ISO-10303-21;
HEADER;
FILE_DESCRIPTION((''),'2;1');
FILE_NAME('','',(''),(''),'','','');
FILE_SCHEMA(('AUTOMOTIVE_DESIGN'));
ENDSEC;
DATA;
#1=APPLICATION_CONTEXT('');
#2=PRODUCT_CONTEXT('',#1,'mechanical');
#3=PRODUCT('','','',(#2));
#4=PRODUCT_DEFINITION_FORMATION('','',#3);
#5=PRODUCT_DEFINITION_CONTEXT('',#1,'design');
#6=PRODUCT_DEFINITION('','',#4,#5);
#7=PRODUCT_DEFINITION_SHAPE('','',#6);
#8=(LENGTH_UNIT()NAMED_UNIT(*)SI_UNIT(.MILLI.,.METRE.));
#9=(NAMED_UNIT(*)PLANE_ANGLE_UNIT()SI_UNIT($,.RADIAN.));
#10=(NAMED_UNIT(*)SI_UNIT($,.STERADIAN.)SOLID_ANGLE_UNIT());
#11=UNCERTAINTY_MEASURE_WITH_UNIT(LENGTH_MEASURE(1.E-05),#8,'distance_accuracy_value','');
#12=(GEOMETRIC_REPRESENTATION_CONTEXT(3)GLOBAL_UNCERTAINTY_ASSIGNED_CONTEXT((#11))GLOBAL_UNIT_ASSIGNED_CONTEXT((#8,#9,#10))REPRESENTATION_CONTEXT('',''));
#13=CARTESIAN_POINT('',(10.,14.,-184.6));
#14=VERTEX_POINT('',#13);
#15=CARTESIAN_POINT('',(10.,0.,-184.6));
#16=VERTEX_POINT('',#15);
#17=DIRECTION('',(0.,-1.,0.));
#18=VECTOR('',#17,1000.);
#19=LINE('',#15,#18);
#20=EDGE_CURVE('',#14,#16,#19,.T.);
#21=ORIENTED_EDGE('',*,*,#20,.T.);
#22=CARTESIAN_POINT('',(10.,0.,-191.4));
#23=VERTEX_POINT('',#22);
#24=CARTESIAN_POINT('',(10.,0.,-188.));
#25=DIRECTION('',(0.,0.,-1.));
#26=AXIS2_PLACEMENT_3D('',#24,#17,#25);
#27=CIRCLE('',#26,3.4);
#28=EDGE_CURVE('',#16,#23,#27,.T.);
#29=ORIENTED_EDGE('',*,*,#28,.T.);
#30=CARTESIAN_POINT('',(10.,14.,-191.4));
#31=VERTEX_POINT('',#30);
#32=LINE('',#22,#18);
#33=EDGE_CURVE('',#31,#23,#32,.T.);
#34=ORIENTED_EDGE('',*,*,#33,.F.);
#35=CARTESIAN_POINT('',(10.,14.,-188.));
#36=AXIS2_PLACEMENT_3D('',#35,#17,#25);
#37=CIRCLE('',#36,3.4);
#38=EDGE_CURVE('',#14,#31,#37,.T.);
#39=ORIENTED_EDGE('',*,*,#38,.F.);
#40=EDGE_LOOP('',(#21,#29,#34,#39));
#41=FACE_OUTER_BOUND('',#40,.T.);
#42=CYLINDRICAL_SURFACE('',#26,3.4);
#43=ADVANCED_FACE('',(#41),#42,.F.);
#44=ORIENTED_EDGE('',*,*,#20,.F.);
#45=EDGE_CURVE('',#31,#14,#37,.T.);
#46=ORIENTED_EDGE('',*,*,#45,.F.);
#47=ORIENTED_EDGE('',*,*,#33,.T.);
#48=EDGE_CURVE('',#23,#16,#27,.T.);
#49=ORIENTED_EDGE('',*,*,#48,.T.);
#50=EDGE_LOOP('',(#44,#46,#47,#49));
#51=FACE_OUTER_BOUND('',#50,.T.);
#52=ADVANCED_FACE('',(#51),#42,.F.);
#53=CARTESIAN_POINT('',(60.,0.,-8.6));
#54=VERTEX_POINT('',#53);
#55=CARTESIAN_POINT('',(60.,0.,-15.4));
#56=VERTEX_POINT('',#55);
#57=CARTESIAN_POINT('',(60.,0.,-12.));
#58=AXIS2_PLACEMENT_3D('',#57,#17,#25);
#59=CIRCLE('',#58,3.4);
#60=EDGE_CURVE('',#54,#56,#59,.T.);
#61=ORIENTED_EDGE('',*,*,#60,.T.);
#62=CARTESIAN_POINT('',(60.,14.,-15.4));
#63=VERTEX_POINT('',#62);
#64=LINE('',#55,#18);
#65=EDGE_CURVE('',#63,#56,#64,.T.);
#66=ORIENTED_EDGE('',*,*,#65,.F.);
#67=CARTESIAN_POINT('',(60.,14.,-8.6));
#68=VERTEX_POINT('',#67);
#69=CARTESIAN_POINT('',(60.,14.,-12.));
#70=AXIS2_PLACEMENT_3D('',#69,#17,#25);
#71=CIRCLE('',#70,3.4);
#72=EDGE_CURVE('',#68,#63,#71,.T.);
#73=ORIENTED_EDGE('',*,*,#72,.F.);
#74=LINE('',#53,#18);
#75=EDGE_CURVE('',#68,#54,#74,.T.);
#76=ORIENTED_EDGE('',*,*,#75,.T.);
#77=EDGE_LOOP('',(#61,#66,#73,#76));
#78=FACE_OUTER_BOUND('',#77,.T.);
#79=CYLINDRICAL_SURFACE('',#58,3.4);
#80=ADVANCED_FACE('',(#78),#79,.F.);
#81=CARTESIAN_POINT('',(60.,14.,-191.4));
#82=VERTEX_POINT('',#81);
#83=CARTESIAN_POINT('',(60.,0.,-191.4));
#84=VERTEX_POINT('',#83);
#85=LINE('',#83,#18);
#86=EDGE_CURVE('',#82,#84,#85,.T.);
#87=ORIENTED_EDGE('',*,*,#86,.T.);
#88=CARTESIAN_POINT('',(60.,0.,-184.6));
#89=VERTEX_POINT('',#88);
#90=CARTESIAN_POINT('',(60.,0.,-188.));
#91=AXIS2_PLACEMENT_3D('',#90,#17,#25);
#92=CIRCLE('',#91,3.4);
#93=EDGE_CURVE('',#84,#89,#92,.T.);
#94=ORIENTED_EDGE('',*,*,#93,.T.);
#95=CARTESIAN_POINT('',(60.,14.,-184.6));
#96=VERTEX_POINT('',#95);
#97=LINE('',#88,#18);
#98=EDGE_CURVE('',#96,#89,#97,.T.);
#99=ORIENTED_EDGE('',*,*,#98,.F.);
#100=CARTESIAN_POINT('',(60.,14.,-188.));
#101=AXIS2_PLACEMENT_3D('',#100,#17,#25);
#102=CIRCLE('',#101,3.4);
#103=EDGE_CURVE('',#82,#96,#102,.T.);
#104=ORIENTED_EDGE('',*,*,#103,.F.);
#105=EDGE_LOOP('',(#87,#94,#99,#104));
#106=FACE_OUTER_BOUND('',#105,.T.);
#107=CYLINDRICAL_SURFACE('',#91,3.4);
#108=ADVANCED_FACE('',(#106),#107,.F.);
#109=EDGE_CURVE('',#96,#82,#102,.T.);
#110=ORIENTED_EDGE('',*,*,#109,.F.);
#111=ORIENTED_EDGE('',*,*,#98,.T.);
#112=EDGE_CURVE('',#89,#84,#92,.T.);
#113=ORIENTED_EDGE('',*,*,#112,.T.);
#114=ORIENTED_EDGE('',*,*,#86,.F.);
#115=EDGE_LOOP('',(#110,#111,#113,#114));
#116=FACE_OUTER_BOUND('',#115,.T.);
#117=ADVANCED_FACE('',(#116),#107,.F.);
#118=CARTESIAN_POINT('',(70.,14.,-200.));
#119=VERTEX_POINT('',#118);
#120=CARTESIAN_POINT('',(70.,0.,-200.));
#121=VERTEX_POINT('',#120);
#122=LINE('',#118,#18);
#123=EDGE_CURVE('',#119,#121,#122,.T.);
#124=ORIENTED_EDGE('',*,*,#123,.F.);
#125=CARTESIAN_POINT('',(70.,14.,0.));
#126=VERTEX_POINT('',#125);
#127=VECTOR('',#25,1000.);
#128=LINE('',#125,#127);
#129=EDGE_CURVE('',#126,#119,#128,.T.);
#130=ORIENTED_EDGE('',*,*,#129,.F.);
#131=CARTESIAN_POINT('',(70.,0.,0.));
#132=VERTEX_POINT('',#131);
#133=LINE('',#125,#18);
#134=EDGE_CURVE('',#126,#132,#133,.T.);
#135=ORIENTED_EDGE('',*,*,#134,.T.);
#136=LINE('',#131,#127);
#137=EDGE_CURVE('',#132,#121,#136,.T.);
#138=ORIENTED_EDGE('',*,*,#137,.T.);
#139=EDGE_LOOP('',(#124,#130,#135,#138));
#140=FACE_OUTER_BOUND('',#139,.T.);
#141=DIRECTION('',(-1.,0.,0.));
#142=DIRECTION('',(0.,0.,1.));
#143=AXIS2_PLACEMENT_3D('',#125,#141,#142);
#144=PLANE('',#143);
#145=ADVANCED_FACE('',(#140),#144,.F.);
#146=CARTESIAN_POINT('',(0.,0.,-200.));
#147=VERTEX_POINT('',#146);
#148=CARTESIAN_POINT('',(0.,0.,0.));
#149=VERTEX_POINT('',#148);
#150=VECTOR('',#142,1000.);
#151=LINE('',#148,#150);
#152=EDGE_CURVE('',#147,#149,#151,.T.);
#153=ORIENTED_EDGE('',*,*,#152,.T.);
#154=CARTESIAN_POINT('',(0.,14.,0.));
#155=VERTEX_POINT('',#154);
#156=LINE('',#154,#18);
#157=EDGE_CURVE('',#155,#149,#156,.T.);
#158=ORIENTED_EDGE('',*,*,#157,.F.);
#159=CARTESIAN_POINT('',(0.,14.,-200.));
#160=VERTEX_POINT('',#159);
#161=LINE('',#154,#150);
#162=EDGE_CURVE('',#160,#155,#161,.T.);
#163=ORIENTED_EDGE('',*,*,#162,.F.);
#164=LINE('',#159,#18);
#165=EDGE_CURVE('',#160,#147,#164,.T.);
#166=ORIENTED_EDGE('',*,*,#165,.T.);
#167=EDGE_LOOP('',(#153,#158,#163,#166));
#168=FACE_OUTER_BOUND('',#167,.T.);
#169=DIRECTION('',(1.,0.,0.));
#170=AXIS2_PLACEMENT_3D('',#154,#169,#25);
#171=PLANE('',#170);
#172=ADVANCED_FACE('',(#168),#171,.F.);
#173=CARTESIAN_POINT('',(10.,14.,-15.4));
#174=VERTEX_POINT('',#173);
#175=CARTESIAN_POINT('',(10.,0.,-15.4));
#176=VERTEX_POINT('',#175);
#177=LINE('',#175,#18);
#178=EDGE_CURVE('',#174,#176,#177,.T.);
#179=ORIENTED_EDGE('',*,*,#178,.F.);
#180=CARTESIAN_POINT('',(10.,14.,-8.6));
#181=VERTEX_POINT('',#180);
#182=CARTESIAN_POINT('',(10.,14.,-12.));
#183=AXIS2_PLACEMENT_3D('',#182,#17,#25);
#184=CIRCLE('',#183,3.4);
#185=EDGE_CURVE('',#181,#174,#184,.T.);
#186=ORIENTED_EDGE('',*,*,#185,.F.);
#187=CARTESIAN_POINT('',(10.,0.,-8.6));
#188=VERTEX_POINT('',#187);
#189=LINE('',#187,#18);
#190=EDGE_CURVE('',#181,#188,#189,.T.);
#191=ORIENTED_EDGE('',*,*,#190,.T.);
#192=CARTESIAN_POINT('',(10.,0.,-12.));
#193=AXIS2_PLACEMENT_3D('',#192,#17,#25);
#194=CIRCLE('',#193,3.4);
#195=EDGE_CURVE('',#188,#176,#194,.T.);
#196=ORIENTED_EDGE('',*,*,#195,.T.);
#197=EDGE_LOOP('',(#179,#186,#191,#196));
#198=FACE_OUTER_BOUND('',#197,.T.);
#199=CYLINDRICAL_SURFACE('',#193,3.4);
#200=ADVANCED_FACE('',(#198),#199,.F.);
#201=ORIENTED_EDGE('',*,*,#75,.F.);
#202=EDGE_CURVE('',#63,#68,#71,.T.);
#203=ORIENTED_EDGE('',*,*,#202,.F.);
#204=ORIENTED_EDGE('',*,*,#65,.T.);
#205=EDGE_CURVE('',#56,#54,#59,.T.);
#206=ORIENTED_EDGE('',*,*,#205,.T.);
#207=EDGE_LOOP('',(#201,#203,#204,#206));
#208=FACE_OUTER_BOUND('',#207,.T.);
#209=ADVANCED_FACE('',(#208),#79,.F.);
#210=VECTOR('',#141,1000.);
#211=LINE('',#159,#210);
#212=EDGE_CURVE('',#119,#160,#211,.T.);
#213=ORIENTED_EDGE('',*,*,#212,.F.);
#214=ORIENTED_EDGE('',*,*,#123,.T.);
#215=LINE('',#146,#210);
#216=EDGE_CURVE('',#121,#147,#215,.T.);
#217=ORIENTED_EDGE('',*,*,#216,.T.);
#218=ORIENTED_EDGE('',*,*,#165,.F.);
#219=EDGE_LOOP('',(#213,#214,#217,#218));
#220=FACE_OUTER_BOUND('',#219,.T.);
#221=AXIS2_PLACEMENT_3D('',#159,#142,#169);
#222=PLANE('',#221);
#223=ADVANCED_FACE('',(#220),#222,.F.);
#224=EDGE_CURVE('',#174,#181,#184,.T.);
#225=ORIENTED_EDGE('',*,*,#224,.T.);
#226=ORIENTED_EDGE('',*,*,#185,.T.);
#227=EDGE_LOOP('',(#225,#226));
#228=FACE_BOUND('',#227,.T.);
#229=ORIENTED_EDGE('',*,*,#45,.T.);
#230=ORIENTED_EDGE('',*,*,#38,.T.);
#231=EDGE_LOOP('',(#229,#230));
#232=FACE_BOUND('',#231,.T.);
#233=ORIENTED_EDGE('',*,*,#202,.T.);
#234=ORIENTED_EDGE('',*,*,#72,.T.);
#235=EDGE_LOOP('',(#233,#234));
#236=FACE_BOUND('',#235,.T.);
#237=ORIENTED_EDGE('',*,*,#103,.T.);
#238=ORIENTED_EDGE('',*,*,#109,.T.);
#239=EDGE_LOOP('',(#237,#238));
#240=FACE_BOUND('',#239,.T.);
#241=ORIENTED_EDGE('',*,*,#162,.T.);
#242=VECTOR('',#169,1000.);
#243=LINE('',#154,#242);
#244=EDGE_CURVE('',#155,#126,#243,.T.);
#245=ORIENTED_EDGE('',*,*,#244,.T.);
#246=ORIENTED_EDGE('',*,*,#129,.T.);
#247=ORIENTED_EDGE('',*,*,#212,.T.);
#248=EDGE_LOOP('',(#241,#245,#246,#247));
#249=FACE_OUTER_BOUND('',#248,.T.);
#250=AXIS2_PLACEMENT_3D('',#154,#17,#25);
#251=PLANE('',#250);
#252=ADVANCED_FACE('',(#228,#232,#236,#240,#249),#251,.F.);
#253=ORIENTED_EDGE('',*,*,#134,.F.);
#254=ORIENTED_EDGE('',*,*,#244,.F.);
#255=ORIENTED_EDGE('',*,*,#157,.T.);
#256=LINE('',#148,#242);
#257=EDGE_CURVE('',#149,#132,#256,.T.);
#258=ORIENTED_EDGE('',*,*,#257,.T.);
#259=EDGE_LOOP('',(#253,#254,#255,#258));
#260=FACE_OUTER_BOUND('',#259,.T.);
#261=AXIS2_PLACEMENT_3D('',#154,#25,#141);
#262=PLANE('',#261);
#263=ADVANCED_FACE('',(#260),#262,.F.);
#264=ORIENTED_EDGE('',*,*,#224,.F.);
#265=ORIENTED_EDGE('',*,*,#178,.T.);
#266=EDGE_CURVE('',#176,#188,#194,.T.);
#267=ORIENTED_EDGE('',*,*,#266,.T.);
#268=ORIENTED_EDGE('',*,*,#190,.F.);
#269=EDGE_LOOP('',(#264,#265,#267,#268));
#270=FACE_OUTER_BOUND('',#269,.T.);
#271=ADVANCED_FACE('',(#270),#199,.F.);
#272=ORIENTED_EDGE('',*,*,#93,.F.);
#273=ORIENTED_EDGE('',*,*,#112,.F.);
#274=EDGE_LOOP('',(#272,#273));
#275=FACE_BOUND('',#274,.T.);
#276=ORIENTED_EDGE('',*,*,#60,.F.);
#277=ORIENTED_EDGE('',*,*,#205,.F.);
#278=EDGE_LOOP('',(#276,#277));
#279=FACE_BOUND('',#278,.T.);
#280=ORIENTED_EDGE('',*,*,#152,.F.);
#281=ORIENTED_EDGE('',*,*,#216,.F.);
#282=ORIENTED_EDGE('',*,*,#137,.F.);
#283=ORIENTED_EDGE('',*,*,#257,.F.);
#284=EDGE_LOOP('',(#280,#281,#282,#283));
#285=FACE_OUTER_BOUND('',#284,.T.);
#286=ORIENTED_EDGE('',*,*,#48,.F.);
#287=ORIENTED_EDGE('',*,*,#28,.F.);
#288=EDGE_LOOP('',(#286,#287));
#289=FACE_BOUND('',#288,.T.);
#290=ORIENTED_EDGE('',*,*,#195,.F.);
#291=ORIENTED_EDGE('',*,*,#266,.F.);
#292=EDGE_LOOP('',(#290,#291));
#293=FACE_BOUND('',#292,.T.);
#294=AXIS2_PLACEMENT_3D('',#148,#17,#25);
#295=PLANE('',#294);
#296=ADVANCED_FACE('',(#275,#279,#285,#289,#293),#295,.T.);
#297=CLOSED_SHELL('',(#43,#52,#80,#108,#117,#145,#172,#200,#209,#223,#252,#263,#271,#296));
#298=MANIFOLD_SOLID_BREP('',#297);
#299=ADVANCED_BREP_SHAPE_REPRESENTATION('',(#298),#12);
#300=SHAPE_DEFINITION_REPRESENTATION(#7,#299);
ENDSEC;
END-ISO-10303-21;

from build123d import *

# Parameters (mm, degrees)
SKETCH1_W           = 70
SKETCH1_H           = 200
BOSS_EXTRUDE1_DEPTH = 14
M8_TAPPED_HOLE1_D   = 6.8


with BuildPart() as part:
    # Sketch1 → Boss-Extrude1 (new body)
    with BuildSketch(Plane(origin=(0, 0, 0), x_dir=(1, 0, 0), z_dir=(0, 1, 0))):
        with Locations((35, 100)):
            Rectangle(SKETCH1_W, SKETCH1_H)
    extrude(amount=BOSS_EXTRUDE1_DEPTH)

    # M8 Tapped Hole1 (through all)
    with Locations(Plane(origin=(0, 0, 0), x_dir=(-1, 0, 0), z_dir=(0, -1, 0))):
        with Locations((-60, 188), (-10, 188), (-10, 12), (-60, 12)):
            Hole(M8_TAPPED_HOLE1_D / 2)


solid = part.part
